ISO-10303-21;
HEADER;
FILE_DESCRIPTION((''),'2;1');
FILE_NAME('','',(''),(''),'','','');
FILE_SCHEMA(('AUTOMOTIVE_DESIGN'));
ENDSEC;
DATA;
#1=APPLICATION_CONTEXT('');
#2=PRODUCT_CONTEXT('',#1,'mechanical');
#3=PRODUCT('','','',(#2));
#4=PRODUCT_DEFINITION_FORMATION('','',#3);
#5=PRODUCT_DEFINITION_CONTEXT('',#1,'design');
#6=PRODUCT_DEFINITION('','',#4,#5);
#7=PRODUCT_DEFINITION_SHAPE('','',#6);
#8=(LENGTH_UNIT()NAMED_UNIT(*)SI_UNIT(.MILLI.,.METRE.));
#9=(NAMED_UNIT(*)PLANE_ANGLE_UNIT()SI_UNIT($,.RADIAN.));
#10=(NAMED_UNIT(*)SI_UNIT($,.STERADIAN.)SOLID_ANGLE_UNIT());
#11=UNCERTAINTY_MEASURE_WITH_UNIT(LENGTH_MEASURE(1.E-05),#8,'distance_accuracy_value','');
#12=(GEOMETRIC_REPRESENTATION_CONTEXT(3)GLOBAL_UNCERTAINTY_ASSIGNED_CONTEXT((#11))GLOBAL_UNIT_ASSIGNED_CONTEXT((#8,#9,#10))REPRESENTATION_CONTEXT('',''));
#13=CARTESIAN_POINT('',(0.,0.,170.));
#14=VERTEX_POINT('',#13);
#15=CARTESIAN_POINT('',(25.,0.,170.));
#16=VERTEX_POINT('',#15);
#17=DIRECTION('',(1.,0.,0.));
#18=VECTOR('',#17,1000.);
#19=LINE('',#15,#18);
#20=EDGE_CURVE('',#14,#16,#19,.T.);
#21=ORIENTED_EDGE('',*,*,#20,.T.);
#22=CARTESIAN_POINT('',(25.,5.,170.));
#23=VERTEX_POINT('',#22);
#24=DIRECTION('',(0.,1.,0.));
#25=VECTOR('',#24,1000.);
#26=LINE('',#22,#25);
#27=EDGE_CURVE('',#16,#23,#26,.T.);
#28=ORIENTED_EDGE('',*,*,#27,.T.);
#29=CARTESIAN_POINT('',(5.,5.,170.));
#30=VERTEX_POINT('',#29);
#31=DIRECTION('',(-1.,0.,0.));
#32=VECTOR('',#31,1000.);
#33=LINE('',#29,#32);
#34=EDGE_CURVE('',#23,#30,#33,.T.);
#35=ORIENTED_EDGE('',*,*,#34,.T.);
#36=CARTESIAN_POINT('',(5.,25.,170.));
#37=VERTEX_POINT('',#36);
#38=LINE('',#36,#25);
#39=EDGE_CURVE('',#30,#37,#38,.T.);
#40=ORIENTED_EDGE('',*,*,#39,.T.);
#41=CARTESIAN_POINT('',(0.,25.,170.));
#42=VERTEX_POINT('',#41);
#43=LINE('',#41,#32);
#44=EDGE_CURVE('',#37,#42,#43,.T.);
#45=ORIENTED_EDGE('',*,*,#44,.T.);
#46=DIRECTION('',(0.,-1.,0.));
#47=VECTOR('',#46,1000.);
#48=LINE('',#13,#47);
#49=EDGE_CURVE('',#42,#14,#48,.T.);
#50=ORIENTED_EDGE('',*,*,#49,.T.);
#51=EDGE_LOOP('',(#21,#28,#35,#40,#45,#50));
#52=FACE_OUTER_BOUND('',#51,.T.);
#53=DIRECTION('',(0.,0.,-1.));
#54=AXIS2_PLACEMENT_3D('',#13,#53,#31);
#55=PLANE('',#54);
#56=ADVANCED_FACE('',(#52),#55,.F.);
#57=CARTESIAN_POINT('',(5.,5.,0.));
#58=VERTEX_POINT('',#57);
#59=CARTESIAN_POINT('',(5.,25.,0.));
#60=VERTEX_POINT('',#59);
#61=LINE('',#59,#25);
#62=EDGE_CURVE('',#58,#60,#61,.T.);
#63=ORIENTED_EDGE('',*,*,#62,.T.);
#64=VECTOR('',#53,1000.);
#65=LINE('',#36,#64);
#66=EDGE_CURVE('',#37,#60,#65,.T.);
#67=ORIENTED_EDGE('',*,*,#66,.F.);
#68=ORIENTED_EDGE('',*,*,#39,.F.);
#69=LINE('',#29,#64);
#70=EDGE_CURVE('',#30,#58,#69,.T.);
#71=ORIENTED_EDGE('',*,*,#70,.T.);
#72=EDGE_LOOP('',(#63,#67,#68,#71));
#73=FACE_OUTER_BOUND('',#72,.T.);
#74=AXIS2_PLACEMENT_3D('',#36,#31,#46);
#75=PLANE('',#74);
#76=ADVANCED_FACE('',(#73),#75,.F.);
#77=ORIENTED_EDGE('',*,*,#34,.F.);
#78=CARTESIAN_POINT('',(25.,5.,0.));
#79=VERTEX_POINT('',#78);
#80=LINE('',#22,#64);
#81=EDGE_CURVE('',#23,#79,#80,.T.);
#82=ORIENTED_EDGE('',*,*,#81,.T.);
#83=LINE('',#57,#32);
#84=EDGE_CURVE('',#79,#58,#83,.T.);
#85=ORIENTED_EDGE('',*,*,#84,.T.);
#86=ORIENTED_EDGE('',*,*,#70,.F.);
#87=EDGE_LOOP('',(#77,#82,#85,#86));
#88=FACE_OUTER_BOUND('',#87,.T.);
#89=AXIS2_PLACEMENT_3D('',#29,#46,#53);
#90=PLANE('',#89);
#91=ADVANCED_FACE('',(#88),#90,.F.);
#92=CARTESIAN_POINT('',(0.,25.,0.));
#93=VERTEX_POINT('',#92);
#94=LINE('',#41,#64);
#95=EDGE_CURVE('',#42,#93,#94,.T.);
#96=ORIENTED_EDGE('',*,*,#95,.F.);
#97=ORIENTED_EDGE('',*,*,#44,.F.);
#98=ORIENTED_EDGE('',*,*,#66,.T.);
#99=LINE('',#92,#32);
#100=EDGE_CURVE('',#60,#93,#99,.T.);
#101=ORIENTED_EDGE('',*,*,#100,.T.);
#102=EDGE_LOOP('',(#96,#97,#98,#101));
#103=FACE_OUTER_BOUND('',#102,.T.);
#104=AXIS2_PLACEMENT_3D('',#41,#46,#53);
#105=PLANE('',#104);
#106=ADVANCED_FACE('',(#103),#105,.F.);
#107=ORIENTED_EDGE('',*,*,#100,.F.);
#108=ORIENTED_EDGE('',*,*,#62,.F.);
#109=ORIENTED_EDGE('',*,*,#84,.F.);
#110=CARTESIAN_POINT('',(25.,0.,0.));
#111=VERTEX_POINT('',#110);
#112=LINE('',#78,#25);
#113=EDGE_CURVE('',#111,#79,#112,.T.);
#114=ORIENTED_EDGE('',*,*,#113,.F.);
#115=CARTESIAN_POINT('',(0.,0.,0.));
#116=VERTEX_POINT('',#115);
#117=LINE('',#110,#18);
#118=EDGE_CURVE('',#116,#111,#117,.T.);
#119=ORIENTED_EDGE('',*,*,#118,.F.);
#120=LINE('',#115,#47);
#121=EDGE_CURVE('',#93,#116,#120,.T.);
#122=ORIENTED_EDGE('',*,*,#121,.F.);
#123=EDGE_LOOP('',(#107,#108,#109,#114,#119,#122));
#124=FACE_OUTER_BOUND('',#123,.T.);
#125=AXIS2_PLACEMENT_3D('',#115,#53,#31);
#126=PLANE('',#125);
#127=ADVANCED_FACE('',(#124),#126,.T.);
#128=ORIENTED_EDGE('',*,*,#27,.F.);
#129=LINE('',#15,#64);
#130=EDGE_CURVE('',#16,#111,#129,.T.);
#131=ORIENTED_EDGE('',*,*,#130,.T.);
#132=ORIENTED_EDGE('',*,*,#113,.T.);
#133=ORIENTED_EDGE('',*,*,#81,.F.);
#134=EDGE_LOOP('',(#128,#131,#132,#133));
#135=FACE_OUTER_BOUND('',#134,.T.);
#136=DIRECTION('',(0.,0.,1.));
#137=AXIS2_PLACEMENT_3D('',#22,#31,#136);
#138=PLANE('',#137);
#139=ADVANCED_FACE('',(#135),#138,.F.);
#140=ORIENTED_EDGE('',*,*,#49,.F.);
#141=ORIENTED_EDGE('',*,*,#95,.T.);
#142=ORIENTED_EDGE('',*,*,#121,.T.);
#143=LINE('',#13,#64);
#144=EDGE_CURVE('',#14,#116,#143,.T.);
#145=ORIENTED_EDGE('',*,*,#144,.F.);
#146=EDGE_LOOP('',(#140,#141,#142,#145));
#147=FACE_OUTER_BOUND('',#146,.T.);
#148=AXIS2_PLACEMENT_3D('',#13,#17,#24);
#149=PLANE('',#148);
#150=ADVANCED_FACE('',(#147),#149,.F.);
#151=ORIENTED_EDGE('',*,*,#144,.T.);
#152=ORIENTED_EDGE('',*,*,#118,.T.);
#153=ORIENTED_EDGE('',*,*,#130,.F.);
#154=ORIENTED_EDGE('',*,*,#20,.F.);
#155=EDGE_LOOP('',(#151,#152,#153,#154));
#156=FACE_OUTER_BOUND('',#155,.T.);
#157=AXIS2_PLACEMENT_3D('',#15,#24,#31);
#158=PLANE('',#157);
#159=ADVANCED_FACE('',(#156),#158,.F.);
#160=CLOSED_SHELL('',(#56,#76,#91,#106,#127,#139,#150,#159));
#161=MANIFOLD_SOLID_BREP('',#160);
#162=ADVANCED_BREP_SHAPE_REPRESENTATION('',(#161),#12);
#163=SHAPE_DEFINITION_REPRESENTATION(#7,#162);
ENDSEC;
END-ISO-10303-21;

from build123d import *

# Parameters (mm, degrees)
EXTRUDE_1_DEPTH = 170


with BuildPart() as part:
    # 草图1 → 凸台-拉伸1 (new body)
    with BuildSketch(Plane.XY):
        Polygon((0, 0), (0, 25), (5, 25), (5, 5), (25, 5), (25, 0), align=None)
    extrude(amount=EXTRUDE_1_DEPTH)


solid = part.part
